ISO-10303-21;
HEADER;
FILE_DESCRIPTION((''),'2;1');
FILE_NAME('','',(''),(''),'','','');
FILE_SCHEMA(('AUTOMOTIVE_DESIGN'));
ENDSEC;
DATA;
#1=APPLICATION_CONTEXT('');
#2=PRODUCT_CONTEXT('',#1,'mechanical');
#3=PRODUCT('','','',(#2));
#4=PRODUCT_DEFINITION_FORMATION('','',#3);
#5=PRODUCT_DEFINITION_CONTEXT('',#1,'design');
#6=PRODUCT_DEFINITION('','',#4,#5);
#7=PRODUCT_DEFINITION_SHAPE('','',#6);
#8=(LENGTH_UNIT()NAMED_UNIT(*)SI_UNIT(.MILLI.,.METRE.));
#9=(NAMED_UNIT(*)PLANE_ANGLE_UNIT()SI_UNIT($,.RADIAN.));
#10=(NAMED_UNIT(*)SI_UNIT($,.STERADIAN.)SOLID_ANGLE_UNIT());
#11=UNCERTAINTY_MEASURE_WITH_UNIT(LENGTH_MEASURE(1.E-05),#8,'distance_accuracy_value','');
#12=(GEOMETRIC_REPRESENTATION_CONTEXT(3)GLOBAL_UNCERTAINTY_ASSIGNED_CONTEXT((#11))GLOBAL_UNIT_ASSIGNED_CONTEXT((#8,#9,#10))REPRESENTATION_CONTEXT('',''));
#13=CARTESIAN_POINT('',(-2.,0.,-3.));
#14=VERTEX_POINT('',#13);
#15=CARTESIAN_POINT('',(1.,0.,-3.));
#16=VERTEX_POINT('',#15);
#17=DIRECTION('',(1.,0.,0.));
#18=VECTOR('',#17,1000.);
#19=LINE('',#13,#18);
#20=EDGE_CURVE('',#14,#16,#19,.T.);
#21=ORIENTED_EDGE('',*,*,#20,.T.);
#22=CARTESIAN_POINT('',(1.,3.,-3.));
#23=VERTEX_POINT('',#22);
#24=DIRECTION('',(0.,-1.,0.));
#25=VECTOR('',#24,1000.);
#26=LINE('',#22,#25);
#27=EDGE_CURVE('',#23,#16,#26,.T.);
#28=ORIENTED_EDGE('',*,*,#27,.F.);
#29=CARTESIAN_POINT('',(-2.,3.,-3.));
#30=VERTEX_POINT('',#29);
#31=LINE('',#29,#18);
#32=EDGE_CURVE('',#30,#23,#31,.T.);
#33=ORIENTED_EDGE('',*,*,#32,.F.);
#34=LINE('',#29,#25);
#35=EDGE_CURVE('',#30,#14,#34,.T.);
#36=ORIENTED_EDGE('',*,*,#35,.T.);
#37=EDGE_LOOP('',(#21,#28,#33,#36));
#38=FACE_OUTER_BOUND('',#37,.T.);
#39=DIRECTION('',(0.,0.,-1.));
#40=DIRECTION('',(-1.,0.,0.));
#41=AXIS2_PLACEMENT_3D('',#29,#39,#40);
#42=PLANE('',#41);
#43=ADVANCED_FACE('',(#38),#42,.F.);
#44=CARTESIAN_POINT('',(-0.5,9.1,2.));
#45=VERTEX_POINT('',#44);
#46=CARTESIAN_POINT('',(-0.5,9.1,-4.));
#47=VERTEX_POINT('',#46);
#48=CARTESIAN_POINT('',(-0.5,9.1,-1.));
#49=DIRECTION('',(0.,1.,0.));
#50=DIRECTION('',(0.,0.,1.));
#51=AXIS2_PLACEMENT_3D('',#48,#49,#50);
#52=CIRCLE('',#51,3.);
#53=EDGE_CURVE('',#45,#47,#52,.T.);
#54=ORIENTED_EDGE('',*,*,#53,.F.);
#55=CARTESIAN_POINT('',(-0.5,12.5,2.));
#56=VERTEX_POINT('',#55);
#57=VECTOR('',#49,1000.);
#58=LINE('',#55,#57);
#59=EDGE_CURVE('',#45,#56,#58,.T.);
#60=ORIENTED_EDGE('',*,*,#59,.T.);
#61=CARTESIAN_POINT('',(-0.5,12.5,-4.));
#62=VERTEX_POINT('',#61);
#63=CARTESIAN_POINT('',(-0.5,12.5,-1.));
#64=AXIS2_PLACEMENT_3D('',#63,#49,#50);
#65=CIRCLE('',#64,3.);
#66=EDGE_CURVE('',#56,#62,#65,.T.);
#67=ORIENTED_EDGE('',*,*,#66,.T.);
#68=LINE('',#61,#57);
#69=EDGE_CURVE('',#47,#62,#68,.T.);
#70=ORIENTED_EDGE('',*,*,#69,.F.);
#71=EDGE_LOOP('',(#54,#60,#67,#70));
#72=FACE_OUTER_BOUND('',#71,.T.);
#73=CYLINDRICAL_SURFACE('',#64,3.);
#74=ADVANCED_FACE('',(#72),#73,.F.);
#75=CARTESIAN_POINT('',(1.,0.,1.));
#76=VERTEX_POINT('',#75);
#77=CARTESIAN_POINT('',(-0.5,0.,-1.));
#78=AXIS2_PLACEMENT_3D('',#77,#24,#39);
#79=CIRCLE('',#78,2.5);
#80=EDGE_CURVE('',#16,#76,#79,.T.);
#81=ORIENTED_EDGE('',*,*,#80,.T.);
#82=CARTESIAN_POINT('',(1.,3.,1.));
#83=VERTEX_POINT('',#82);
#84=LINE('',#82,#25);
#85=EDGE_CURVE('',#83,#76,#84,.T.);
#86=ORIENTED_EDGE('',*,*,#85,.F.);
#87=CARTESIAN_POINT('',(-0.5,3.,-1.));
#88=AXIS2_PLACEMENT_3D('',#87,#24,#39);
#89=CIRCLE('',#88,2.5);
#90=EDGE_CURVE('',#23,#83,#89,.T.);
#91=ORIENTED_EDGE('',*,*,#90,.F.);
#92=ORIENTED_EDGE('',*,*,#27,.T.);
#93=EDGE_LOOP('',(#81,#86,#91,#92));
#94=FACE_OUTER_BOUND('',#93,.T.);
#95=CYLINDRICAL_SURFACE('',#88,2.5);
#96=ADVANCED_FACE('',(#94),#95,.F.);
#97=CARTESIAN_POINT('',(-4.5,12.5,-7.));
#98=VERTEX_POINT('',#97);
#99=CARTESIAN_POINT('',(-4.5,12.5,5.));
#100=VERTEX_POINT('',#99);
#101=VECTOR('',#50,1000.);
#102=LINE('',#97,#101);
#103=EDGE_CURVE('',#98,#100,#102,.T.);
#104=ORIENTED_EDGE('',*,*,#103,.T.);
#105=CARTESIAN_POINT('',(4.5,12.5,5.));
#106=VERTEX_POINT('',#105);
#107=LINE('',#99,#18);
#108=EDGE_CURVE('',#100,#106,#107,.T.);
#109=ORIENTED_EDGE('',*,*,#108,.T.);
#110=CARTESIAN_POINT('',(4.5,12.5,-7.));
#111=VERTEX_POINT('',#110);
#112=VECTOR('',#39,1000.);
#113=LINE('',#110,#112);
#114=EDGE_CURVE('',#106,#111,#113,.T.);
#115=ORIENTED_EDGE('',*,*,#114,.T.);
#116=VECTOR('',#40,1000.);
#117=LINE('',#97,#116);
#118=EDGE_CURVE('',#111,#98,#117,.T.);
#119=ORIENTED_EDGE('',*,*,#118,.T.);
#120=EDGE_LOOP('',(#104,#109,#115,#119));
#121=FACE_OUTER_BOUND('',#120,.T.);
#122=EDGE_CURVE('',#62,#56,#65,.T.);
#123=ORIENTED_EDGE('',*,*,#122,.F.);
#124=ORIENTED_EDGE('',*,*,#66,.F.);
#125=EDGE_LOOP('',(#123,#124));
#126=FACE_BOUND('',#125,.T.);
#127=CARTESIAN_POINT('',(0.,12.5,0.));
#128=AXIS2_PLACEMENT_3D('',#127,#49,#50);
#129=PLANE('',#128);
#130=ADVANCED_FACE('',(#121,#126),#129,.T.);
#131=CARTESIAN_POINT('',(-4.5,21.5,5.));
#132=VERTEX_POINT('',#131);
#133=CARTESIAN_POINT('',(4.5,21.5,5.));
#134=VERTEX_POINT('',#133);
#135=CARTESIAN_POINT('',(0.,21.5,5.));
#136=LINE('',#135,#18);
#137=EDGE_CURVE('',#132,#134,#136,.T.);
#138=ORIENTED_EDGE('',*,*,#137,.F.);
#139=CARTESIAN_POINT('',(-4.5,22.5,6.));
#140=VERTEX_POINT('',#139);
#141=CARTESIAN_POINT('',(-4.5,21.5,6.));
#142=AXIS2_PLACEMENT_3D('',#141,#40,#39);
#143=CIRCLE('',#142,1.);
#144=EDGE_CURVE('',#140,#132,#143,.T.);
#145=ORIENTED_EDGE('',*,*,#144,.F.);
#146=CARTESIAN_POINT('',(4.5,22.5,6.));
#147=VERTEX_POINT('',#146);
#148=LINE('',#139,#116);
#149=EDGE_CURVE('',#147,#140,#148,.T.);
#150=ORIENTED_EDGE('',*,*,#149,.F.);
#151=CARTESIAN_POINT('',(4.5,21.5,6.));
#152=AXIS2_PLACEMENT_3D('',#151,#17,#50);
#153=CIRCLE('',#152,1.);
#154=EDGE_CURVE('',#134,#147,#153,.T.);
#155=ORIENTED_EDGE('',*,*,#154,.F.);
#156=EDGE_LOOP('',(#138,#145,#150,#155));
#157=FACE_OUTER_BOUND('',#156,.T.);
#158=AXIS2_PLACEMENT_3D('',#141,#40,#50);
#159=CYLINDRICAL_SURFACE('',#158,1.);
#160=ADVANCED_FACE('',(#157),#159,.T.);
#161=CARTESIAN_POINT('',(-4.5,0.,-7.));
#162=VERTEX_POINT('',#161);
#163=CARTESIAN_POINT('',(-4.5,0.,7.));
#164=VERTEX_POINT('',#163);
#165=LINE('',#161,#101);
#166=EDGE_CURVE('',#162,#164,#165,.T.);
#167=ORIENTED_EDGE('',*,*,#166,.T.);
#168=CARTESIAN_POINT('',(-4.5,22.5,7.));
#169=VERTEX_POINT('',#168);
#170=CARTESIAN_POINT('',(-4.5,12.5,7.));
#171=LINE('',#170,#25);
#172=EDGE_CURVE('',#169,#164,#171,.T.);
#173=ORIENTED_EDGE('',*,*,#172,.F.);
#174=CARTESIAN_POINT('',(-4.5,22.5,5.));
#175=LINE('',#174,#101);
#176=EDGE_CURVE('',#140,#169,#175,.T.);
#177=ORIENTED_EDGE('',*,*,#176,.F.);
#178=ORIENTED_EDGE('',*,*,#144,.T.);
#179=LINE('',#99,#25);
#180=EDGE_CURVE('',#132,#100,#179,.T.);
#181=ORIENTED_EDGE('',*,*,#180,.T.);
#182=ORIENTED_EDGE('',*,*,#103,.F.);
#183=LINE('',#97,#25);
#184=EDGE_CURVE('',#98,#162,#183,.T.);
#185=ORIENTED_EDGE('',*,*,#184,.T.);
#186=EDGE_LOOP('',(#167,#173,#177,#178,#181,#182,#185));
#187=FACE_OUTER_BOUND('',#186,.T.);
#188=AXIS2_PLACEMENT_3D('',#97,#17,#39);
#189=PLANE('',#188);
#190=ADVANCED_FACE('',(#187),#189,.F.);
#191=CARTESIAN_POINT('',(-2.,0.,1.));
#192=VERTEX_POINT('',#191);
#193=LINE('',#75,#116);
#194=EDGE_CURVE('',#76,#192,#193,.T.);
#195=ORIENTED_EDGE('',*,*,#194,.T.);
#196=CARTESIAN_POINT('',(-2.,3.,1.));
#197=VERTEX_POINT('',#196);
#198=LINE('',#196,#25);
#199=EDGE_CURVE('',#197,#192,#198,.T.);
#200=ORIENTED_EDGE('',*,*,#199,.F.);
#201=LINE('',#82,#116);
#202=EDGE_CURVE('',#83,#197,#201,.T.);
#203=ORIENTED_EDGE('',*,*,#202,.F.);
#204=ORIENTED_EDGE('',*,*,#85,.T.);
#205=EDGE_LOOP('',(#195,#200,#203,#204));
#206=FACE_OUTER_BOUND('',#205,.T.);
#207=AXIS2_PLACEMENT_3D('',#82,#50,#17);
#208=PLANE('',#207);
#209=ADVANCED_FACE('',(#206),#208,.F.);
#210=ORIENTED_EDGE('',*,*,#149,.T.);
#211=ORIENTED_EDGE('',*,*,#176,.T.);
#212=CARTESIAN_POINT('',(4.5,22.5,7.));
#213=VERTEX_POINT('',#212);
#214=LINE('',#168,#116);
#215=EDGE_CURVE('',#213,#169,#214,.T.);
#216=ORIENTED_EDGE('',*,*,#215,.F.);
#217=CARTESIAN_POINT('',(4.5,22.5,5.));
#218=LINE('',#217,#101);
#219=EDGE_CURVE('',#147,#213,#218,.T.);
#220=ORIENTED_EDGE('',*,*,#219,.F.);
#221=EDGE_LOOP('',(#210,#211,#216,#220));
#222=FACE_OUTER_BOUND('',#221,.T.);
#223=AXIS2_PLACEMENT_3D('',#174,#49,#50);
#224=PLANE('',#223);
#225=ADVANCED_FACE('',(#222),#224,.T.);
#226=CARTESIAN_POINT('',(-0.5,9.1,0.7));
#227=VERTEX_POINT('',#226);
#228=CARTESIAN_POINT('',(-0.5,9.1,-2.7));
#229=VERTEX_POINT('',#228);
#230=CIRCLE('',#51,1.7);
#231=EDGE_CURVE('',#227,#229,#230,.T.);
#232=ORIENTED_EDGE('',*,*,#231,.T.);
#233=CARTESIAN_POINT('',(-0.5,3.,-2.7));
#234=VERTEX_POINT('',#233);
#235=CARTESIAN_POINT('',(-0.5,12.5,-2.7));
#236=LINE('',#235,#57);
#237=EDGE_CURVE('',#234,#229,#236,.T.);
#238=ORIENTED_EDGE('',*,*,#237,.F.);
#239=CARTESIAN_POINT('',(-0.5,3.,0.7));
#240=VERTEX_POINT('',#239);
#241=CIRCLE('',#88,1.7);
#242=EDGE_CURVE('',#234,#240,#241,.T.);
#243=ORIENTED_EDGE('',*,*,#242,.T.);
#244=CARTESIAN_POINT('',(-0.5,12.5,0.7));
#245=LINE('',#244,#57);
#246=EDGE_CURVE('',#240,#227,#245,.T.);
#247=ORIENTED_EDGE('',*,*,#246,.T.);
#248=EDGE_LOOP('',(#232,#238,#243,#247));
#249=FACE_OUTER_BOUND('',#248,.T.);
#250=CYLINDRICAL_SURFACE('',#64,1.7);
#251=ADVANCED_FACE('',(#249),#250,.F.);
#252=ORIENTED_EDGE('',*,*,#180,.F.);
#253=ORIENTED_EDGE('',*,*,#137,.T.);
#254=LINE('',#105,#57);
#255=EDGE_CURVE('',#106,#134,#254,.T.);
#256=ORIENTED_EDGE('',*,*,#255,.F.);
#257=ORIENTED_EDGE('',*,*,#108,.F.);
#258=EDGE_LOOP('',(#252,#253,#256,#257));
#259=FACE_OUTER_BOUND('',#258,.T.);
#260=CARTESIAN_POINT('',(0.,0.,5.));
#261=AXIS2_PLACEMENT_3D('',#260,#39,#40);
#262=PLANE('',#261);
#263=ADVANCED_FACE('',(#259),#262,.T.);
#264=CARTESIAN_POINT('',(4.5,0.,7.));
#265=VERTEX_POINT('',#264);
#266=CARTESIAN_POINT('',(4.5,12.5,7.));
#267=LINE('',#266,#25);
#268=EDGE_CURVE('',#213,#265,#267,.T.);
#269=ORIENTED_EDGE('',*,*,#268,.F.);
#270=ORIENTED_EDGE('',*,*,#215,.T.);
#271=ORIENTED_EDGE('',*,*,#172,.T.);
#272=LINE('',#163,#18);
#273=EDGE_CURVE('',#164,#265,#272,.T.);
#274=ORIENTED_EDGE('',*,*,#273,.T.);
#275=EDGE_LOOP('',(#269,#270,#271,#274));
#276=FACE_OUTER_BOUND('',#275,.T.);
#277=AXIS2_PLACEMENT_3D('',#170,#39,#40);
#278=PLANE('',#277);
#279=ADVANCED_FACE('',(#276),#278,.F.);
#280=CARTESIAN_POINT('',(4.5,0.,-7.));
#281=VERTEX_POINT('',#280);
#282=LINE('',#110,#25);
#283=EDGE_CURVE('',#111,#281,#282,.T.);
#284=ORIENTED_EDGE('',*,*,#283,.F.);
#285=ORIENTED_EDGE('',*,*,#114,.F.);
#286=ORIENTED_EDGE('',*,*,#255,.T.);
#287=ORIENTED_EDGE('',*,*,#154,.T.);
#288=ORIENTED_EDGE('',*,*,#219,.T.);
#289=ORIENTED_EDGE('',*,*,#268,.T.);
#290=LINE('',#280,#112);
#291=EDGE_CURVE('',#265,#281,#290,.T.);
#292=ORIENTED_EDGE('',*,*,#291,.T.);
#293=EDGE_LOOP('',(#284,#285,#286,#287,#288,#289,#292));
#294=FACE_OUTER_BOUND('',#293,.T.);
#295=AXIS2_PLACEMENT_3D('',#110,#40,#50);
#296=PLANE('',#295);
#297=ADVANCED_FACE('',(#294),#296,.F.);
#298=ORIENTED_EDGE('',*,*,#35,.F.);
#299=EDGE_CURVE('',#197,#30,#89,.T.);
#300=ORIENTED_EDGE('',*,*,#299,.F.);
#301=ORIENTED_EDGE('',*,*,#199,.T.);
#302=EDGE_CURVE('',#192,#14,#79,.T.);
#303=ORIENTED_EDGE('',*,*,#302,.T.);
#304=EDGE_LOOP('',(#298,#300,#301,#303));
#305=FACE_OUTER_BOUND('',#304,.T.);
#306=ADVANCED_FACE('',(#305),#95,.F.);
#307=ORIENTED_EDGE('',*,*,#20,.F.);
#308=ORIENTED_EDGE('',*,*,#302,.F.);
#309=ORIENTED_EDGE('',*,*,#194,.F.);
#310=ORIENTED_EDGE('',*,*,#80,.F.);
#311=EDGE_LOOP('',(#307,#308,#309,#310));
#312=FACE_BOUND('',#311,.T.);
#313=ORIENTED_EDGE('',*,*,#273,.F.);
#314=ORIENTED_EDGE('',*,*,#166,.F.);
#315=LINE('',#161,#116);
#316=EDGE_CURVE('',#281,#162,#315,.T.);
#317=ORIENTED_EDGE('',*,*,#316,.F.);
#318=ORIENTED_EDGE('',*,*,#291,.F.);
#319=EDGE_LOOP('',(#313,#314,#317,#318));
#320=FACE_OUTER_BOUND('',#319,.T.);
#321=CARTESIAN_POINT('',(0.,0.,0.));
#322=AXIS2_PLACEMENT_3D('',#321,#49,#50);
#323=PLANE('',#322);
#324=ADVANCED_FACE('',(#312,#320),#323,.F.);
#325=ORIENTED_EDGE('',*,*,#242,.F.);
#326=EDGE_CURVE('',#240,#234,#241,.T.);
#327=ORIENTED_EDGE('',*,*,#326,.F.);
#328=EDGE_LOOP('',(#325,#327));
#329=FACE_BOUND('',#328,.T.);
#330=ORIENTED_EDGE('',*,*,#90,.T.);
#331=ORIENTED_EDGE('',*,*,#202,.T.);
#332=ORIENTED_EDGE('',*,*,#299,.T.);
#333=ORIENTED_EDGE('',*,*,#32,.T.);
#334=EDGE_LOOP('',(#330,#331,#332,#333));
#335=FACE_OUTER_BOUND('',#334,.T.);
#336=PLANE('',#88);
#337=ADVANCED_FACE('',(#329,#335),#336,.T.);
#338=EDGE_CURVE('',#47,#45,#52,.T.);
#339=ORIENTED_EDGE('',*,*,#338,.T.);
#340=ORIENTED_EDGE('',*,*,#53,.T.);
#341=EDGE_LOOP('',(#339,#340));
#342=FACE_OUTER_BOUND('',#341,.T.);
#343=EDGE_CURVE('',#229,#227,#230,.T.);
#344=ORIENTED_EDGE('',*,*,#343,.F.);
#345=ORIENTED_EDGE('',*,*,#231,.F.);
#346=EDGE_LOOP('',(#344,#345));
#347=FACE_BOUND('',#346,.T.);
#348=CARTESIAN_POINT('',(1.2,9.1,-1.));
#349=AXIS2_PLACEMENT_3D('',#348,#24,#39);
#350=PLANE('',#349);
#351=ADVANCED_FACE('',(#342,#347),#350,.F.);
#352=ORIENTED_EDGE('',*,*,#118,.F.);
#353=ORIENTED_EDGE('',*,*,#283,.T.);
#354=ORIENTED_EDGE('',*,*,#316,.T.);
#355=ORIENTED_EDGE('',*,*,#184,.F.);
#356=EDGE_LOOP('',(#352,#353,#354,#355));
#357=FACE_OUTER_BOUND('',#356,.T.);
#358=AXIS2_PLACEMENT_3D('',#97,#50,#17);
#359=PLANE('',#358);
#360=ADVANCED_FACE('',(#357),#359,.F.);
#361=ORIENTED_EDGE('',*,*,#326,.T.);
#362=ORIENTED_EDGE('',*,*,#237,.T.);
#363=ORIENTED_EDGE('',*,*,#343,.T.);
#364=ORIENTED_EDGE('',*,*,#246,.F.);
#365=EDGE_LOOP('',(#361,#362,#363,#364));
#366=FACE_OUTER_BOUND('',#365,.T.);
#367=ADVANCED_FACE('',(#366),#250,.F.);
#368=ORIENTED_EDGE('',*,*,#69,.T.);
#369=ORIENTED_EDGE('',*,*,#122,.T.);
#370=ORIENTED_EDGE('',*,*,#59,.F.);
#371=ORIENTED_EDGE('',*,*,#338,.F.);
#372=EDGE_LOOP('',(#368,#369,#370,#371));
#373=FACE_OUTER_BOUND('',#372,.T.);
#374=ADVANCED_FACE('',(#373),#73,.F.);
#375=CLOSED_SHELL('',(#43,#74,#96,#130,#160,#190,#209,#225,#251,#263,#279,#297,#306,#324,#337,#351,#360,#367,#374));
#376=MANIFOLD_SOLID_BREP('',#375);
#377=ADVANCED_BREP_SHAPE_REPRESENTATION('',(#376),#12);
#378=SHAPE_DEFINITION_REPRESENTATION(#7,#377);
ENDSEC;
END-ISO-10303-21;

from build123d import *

# Parameters (mm, degrees)
SKETCH1_W                                         = 9
SKETCH1_H                                         = 14
BOSS_EXTRUDE1_DEPTH                               = 12.5
CUT_EXTRUDE1_DEPTH                                = 3
SKETCH3_W                                         = 9
SKETCH3_H                                         = 10
BOSS_EXTRUDE2_DEPTH                               = 2
FILLET1_R                                         = 1
HOLE_SIZE_PER_HEX_SOCKET_SCREW_TYPE_1_D           = 3.4
HOLE_SIZE_PER_HEX_SOCKET_SCREW_TYPE_1_CBORE_D     = 6
HOLE_SIZE_PER_HEX_SOCKET_SCREW_TYPE_1_CBORE_DEPTH = 3.4


with BuildPart() as part:
    # Sketch1 → Boss-Extrude1 (new body)
    with BuildSketch(Plane(origin=(0, 0, 0), x_dir=(1, 0, 0), z_dir=(0, 1, 0))):
        Rectangle(SKETCH1_W, SKETCH1_H)
    extrude(amount=BOSS_EXTRUDE1_DEPTH)

    # Sketch2 → Cut-Extrude1 (cut)
    with BuildSketch(Plane.XZ):
        with BuildLine():
            Line((1, 1), (-2, 1))
            ThreePointArc((-2, 1), (-3, -1), (-2, -3))
            Line((-2, -3), (1, -3))
            ThreePointArc((1, -3), (2, -1), (1, 1))
        make_face()
    extrude(amount=-CUT_EXTRUDE1_DEPTH, mode=Mode.SUBTRACT)

    # Sketch3 → Boss-Extrude2 (add)
    with BuildSketch(Plane.XY.offset(7)):
        with Locations((0, 17.5)):
            Rectangle(SKETCH3_W, SKETCH3_H)
    extrude(amount=-BOSS_EXTRUDE2_DEPTH)

    # Fillet1
    fillet1_edges = [part.edges().sort_by_distance(p)[0] for p in [
        (0, 22.5, 5),
    ]]
    fillet(fillet1_edges, radius=FILLET1_R)

    # Hole size (per hex socket screw type) 1 (through all)
    with Locations(Plane(origin=(-0.5, 12.5, -1), x_dir=(0, 0, 1), z_dir=(0, 1, 0))):
        with Locations((0, 0)):
            CounterBoreHole(HOLE_SIZE_PER_HEX_SOCKET_SCREW_TYPE_1_D / 2, HOLE_SIZE_PER_HEX_SOCKET_SCREW_TYPE_1_CBORE_D / 2, HOLE_SIZE_PER_HEX_SOCKET_SCREW_TYPE_1_CBORE_DEPTH)


solid = part.part
